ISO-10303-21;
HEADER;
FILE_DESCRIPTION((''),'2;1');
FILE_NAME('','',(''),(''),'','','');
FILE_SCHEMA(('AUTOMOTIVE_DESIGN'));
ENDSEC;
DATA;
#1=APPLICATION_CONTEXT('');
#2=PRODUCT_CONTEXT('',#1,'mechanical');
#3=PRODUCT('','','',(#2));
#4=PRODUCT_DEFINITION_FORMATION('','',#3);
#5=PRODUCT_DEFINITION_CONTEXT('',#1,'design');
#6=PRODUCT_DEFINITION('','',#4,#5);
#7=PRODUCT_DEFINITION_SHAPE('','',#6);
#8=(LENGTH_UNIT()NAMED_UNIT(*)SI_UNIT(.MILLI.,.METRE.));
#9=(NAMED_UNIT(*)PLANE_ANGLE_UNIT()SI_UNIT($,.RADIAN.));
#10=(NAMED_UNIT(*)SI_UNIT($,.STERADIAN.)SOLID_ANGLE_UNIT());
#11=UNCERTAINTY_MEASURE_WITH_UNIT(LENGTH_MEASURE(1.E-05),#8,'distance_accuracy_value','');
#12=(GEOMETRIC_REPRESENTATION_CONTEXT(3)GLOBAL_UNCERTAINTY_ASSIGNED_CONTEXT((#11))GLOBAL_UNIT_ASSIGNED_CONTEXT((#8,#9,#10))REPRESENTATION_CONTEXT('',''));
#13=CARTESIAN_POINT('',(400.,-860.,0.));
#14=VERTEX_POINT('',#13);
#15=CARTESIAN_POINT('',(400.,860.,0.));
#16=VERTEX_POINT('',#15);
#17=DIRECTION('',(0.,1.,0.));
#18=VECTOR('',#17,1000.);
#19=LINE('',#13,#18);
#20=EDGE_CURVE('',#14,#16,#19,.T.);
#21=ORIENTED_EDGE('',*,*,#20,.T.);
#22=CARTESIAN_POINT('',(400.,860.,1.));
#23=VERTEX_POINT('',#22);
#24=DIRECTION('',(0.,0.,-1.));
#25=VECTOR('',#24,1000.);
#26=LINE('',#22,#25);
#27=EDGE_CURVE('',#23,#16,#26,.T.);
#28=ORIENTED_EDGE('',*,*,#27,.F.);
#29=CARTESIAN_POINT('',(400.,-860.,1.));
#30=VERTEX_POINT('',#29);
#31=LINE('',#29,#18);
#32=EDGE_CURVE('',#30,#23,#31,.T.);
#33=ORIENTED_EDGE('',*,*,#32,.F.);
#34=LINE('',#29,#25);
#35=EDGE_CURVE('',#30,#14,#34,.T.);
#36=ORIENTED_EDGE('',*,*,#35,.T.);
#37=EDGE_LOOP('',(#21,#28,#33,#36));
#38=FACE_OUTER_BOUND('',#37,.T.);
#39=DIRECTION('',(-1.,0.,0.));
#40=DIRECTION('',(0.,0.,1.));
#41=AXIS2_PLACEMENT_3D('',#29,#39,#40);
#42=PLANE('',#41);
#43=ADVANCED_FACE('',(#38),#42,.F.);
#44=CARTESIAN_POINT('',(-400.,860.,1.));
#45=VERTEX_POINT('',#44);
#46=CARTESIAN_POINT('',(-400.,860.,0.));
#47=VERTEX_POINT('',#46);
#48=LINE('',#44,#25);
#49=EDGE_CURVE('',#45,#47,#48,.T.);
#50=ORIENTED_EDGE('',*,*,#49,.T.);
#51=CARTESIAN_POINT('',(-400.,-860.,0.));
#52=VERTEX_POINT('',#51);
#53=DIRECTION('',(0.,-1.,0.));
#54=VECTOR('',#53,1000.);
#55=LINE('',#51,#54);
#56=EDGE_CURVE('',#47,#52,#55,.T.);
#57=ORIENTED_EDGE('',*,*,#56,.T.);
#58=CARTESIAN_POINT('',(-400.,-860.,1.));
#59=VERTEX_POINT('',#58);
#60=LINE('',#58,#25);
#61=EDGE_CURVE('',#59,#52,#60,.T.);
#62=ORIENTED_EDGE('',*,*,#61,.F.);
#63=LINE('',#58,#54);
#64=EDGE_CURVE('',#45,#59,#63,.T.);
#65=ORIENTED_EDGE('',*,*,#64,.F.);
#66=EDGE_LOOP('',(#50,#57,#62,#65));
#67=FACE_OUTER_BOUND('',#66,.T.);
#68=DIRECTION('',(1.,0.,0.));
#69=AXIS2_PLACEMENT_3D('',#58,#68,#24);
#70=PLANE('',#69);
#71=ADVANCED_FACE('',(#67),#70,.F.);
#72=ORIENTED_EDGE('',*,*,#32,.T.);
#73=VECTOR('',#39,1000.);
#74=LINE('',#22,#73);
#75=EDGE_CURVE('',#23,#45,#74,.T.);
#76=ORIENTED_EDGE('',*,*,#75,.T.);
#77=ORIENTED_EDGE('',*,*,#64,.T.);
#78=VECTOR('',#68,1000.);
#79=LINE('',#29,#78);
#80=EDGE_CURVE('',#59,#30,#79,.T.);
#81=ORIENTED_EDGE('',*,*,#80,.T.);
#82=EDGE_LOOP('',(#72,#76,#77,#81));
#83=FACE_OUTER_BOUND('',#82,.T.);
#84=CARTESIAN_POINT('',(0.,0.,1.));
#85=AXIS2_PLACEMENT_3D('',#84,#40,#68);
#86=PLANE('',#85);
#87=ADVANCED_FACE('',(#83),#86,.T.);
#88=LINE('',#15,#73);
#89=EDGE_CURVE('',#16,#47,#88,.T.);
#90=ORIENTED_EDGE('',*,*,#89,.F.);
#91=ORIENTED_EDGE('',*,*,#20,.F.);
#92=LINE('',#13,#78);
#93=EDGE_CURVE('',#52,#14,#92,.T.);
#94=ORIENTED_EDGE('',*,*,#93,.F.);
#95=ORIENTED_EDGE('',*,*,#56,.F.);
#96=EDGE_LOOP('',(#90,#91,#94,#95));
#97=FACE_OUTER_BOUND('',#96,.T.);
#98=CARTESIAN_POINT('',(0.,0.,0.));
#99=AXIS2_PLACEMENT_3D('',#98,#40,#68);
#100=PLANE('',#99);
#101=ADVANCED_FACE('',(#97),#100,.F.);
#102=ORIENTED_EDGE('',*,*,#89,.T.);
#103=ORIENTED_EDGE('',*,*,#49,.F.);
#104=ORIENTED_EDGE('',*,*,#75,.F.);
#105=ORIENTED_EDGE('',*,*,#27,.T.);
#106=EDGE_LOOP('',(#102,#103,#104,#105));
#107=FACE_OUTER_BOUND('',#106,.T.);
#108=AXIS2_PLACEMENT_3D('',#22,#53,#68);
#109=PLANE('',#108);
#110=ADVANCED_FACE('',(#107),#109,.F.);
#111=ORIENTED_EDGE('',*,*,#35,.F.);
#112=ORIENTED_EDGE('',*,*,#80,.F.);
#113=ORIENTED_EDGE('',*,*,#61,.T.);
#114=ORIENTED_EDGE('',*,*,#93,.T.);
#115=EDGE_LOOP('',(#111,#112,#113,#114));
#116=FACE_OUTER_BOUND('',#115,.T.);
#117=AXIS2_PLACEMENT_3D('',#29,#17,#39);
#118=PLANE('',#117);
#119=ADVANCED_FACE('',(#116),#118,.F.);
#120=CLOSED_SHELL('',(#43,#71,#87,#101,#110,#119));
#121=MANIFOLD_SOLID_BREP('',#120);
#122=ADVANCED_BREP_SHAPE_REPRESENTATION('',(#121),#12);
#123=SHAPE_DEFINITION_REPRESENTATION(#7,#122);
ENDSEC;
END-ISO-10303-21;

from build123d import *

# Parameters (mm, degrees)
SKETCH1_W           = 800
SKETCH1_H           = 1720
BOSS_EXTRUDE1_DEPTH = 1


with BuildPart() as part:
    # Sketch1 → Boss-Extrude1 (new body)
    with BuildSketch(Plane.XY):
        Rectangle(SKETCH1_W, SKETCH1_H)
    extrude(amount=BOSS_EXTRUDE1_DEPTH)


solid = part.part
